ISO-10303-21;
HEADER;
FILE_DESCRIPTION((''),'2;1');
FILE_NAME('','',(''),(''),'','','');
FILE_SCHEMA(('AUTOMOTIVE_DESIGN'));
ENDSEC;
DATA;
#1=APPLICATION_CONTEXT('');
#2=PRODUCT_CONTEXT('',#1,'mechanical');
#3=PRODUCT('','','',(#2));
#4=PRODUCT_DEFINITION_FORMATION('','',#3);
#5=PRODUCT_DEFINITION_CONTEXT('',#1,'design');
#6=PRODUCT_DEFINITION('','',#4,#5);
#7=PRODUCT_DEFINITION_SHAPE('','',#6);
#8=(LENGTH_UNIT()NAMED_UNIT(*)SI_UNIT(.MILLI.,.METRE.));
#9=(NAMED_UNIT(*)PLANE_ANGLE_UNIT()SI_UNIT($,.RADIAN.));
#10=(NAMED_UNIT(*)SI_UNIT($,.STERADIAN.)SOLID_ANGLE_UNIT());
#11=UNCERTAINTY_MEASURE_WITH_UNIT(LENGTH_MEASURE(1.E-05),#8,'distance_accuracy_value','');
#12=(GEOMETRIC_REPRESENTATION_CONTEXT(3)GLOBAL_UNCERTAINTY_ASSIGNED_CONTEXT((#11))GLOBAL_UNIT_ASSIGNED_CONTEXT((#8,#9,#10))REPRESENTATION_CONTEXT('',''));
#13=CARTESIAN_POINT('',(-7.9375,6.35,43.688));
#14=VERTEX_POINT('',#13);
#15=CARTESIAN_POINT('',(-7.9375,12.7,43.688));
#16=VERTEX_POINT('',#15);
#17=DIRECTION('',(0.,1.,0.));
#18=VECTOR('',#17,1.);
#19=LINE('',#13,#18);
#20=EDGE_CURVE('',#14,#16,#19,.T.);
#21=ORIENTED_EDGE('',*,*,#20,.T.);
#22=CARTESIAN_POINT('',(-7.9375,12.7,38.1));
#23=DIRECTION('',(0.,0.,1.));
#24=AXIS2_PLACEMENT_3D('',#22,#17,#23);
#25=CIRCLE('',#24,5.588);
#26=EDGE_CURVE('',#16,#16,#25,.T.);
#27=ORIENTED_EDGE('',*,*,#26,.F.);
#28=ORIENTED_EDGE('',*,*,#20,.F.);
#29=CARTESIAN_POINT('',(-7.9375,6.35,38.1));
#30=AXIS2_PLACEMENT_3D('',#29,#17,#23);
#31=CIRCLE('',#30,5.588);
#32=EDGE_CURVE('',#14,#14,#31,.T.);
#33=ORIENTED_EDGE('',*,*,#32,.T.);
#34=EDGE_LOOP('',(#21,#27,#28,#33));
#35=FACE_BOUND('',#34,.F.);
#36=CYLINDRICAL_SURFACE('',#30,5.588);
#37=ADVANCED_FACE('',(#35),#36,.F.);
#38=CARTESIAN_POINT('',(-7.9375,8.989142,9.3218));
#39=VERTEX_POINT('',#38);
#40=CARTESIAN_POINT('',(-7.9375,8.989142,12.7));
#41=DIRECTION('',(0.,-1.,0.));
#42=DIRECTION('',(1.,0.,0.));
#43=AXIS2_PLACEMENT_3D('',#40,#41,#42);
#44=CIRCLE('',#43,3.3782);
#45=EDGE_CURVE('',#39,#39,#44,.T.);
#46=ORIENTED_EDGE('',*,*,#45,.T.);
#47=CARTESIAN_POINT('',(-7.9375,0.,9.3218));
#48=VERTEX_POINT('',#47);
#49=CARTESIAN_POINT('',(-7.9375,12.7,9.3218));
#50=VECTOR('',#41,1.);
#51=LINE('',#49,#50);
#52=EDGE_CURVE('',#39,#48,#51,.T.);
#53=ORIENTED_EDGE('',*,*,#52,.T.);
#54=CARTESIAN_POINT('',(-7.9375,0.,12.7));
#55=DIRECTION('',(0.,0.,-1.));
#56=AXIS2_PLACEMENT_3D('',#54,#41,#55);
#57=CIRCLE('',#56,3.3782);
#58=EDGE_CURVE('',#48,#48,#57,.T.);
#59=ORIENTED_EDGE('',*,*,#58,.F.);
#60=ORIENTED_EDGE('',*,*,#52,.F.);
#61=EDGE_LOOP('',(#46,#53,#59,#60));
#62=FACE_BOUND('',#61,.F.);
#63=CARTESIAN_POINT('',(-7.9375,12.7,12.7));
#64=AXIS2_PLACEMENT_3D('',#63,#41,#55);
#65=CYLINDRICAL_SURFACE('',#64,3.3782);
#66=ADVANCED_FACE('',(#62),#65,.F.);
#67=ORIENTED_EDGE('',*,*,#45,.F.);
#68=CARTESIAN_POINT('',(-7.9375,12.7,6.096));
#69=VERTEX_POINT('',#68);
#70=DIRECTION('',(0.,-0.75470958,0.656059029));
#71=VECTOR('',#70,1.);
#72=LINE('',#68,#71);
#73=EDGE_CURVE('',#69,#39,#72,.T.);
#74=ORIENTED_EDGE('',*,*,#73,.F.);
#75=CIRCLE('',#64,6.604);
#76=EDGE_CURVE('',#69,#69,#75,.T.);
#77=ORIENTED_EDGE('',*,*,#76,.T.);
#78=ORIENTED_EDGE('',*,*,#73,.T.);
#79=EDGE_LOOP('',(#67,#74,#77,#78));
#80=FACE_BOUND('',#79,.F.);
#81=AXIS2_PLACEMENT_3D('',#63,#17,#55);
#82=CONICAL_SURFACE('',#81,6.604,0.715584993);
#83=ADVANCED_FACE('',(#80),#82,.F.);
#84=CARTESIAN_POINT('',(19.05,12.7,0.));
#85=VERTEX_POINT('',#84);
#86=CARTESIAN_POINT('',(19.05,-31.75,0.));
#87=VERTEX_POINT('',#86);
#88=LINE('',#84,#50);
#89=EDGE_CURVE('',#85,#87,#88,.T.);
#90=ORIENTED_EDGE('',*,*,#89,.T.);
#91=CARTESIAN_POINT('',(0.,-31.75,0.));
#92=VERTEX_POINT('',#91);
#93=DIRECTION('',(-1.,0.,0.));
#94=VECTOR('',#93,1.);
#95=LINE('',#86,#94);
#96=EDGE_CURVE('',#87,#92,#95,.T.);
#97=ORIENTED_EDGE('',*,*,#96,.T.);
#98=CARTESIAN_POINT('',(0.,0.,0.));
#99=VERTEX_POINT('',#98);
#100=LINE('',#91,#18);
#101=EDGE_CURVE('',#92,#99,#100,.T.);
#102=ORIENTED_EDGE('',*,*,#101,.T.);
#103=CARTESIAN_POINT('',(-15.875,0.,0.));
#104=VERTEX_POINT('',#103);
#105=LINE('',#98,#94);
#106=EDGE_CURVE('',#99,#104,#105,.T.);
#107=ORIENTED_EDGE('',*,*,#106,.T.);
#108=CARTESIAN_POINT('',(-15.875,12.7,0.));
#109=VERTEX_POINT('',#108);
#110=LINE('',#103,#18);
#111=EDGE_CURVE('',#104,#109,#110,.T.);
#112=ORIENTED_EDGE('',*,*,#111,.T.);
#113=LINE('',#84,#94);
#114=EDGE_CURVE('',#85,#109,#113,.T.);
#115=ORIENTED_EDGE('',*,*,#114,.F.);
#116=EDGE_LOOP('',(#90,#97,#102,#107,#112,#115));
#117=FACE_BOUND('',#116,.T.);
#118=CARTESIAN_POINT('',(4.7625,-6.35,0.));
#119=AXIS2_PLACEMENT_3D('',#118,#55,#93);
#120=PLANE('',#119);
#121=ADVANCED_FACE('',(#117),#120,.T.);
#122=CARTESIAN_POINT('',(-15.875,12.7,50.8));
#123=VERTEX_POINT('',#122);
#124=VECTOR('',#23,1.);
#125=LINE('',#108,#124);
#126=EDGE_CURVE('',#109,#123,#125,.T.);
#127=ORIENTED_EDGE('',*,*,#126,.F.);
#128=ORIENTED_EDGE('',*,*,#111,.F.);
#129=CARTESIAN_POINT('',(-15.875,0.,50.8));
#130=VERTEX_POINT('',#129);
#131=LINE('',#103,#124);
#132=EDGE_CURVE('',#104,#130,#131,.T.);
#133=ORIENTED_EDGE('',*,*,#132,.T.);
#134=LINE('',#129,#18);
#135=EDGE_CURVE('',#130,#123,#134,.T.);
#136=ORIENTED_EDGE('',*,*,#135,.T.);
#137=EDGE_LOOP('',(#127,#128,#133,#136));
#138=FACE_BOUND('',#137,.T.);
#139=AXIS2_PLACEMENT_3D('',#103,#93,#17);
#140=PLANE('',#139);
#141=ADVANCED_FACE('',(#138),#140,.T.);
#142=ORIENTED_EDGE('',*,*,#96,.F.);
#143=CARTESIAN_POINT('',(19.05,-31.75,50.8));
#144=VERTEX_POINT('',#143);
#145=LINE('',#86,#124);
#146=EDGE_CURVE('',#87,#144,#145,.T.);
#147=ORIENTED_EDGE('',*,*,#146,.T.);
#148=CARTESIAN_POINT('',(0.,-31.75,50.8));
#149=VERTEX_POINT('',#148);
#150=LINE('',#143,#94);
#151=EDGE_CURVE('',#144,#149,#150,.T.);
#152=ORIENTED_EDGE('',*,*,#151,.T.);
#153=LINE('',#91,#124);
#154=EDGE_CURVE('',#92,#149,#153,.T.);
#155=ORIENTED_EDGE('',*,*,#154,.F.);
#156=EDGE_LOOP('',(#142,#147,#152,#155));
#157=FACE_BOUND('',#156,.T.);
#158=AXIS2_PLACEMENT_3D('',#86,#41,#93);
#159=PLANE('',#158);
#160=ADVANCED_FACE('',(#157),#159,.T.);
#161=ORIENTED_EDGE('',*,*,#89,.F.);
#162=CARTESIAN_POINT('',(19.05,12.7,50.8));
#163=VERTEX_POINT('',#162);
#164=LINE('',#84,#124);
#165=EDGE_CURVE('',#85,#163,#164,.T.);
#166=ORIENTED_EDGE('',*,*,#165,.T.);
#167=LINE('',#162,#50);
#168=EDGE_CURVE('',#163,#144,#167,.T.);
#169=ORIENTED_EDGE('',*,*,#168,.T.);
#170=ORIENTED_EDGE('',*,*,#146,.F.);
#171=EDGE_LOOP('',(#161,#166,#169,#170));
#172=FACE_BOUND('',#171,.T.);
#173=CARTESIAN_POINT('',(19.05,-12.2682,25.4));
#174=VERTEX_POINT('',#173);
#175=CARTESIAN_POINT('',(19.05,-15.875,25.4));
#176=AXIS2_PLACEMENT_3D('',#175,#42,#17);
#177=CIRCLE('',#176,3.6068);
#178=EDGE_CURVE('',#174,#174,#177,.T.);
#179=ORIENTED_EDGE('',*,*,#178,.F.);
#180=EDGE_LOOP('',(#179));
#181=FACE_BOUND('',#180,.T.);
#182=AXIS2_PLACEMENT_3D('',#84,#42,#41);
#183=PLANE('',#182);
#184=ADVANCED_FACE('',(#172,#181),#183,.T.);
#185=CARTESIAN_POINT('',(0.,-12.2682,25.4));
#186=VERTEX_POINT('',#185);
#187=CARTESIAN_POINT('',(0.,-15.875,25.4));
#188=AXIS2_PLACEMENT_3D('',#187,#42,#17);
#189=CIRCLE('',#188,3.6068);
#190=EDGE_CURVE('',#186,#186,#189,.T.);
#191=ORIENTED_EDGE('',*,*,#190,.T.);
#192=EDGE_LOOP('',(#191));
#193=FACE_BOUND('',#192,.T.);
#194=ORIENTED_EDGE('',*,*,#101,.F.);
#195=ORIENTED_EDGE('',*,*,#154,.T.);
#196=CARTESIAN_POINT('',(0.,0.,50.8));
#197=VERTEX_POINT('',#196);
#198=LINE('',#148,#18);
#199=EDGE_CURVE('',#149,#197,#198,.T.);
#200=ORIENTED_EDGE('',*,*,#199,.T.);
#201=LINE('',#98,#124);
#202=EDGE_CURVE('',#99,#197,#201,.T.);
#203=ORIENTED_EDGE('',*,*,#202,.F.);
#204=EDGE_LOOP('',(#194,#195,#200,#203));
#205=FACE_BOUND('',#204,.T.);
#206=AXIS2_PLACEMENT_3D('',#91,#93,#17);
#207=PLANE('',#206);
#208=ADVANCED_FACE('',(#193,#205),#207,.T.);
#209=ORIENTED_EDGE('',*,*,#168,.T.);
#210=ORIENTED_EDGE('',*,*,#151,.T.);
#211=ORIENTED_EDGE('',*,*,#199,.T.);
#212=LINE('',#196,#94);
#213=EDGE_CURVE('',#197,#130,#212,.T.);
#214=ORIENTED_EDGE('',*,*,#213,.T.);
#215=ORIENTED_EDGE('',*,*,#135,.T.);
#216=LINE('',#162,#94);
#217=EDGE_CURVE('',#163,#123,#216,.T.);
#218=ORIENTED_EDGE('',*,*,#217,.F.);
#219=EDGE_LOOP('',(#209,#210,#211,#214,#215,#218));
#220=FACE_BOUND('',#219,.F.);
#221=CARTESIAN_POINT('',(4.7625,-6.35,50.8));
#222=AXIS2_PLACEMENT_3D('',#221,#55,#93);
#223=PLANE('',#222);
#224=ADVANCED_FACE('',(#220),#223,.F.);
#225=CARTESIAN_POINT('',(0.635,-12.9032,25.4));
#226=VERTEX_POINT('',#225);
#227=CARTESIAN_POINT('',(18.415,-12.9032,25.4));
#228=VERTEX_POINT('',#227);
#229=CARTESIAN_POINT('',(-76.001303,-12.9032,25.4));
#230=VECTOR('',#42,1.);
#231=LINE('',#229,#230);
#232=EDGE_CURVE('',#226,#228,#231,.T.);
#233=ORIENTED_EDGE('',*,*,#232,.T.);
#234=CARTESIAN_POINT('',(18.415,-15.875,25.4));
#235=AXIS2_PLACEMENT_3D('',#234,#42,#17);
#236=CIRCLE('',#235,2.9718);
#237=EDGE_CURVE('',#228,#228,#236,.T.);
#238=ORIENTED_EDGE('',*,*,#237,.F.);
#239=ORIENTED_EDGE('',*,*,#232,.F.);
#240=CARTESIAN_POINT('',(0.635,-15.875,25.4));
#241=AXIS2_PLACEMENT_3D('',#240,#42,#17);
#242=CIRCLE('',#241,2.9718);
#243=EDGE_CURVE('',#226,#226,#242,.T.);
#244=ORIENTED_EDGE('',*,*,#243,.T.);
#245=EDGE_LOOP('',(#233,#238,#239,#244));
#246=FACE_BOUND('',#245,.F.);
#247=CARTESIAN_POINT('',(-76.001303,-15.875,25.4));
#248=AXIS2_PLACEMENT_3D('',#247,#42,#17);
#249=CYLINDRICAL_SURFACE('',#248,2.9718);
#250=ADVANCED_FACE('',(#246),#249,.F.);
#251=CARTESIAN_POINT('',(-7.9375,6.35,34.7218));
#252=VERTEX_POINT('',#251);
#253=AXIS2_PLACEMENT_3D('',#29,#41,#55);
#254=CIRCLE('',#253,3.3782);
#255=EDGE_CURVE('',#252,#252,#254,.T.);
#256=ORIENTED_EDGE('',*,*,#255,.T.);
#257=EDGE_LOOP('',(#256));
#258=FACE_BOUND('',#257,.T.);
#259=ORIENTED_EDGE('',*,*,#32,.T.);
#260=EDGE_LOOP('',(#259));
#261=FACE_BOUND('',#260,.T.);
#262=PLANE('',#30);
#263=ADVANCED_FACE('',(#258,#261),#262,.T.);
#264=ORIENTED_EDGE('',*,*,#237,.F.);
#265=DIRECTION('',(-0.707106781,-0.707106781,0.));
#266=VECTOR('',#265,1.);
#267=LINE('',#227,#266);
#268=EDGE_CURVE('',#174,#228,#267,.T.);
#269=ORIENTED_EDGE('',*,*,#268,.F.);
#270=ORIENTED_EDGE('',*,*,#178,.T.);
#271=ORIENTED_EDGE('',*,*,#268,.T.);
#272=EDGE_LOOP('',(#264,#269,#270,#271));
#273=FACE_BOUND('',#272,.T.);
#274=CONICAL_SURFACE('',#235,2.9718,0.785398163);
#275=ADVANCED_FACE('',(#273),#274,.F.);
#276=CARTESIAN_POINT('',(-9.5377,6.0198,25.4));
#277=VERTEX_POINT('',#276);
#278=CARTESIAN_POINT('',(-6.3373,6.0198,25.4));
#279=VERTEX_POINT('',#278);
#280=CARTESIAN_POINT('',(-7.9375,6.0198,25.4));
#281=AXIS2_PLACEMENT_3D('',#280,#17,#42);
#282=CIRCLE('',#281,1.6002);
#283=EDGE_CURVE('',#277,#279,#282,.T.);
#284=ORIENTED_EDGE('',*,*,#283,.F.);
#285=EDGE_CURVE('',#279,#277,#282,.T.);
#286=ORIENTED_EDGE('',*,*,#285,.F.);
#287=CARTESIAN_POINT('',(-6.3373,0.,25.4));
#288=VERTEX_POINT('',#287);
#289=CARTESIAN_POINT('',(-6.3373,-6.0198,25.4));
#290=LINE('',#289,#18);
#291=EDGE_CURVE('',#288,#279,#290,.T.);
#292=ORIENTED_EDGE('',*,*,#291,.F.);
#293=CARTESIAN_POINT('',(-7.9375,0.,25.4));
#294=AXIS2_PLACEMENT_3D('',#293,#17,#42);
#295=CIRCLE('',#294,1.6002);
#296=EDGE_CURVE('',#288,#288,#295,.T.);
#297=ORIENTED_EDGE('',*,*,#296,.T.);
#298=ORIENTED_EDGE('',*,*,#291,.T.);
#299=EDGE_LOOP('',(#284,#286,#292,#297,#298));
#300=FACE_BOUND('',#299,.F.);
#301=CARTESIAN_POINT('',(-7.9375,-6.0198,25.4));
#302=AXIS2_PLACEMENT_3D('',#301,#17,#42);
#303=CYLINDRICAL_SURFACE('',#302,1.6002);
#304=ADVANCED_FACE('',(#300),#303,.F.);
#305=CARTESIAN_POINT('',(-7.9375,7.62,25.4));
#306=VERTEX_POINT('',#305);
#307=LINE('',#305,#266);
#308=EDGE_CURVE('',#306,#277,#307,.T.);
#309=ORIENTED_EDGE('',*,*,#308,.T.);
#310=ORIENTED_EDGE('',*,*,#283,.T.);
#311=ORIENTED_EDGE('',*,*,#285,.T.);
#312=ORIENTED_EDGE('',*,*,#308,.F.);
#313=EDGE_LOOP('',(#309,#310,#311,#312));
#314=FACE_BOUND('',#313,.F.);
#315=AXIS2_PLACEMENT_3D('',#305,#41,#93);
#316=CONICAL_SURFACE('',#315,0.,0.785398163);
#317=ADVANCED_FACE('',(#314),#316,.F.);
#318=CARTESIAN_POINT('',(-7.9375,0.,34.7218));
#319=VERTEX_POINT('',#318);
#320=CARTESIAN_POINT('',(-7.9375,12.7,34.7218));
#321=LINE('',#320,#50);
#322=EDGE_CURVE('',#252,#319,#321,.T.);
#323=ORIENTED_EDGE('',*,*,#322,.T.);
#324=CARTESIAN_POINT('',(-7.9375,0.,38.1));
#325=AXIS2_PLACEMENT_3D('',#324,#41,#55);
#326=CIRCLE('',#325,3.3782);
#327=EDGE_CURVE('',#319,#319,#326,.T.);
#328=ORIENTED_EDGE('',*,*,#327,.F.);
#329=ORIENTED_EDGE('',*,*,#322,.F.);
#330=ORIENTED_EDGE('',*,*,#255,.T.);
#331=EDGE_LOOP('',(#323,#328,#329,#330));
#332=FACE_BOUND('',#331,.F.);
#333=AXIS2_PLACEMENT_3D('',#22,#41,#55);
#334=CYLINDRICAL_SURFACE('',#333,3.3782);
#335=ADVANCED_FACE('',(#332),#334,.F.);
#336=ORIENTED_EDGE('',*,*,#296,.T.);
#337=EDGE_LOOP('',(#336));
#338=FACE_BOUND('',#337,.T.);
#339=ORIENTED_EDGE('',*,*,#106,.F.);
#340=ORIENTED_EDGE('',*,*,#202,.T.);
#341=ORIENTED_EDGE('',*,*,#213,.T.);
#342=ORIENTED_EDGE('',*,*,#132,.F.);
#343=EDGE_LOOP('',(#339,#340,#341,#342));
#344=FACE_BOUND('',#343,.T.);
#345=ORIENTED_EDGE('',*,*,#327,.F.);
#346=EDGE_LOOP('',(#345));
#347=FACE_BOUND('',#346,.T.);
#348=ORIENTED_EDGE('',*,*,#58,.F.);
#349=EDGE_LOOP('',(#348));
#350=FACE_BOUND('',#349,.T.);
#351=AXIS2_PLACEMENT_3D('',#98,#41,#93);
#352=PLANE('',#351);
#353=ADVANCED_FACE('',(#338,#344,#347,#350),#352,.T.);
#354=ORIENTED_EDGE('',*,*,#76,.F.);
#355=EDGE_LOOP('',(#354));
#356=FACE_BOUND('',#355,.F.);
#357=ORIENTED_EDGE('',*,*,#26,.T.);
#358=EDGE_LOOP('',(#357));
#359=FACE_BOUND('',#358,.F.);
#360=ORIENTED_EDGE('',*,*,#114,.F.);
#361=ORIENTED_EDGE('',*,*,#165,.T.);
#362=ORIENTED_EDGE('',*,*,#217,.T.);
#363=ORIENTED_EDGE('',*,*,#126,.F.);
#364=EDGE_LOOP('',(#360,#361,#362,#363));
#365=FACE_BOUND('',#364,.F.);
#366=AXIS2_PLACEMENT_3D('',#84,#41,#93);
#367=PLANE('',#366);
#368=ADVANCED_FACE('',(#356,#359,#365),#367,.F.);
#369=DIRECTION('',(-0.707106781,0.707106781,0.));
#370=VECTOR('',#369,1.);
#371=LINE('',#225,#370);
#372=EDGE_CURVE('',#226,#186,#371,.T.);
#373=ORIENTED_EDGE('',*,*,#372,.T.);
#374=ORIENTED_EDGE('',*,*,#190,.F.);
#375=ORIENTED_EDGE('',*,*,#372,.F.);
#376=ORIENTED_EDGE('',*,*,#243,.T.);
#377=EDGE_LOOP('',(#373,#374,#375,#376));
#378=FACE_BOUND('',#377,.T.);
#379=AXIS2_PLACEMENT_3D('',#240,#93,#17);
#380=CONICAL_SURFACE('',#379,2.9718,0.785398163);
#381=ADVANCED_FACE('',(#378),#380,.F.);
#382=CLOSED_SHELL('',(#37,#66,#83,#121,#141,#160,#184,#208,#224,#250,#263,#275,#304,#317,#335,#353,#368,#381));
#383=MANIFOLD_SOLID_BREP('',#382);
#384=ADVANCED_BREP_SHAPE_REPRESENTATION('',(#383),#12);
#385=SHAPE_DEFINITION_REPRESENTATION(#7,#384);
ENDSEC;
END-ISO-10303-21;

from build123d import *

# Parameters (mm, degrees)
BLOCK_BODY_2IN_DEPTH                      = 50.8
SIDE_THROUGH_HOLE_0_234_D                 = 5.9436
SIDE_HOLE_EDGE_CHAMFER_SIZE               = 0.635
DOWEL_HOLE_0_126_D                        = 3.2004
DOWEL_HOLE_0_126_DEPTH                    = 6.0198
DOWEL_HOLE_0_126_TIP                      = 1.6002
COUNTERSUNK_SCREW_HOLE_NO0_D              = 6.7564
COUNTERSUNK_SCREW_HOLE_NO0_CSINK_D        = 13.208
COUNTERSUNK_SCREW_HOLE_NO0_CSINK_ANGLE    = 82
COUNTERBORED_BOLT_HOLE_0_25IN_D           = 6.7564
COUNTERBORED_BOLT_HOLE_0_25IN_CBORE_D     = 11.176
COUNTERBORED_BOLT_HOLE_0_25IN_CBORE_DEPTH = 6.35


with BuildPart() as part:
    # Block Profile Sketch → Block Body 2in (new body)
    with BuildSketch(Plane.XY):
        Polygon((0, 12.7), (19.05, 12.7), (19.05, -31.75), (0, -31.75), (0, 0), (-15.875, 0), (-15.875, 12.7), align=None)
    extrude(amount=BLOCK_BODY_2IN_DEPTH)

    # Side Through Hole Ø0.234 (through all)
    with Locations(Plane(origin=(0, -15.875, 25.4), x_dir=(0, -1, 0), z_dir=(-1, 0, 0))):
        with Locations((0, 0)):
            Hole(SIDE_THROUGH_HOLE_0_234_D / 2)

    # Side Hole Edge Chamfer
    side_hole_edge_chamfer_edges = [part.edges().sort_by_distance(p)[0] for p in [
        (0, -18.8468, 25.4),
        (19.05, -18.8468, 25.4),
    ]]
    chamfer(side_hole_edge_chamfer_edges, length=SIDE_HOLE_EDGE_CHAMFER_SIZE)

    # Dowel Hole Ø0.126
    with Locations(Plane(origin=(-7.9375, 0, 25.4), x_dir=(-1, 0, 0), z_dir=(0, -1, 0))):
        with Locations((0, 0)):
            Hole(DOWEL_HOLE_0_126_D / 2, depth=DOWEL_HOLE_0_126_DEPTH)
            with Locations((0, 0, -(DOWEL_HOLE_0_126_DEPTH + DOWEL_HOLE_0_126_TIP / 2))):  # 90° drill point
                Cone(0, DOWEL_HOLE_0_126_D / 2, DOWEL_HOLE_0_126_TIP, mode=Mode.SUBTRACT)

    # Countersunk Screw Hole No0 (through all)
    with Locations(Plane(origin=(-7.9375, 12.7, 12.7), x_dir=(0, 0, 1), z_dir=(0, 1, 0))):
        with Locations((0, 0)):
            CounterSinkHole(COUNTERSUNK_SCREW_HOLE_NO0_D / 2, COUNTERSUNK_SCREW_HOLE_NO0_CSINK_D / 2, counter_sink_angle=COUNTERSUNK_SCREW_HOLE_NO0_CSINK_ANGLE)

    # Counterbored Bolt Hole 0.25in (through all)
    with Locations(Plane(origin=(-7.9375, 12.7, 38.1), x_dir=(0, 0, 1), z_dir=(0, 1, 0))):
        with Locations((0, 0)):
            CounterBoreHole(COUNTERBORED_BOLT_HOLE_0_25IN_D / 2, COUNTERBORED_BOLT_HOLE_0_25IN_CBORE_D / 2, COUNTERBORED_BOLT_HOLE_0_25IN_CBORE_DEPTH)


solid = part.part
